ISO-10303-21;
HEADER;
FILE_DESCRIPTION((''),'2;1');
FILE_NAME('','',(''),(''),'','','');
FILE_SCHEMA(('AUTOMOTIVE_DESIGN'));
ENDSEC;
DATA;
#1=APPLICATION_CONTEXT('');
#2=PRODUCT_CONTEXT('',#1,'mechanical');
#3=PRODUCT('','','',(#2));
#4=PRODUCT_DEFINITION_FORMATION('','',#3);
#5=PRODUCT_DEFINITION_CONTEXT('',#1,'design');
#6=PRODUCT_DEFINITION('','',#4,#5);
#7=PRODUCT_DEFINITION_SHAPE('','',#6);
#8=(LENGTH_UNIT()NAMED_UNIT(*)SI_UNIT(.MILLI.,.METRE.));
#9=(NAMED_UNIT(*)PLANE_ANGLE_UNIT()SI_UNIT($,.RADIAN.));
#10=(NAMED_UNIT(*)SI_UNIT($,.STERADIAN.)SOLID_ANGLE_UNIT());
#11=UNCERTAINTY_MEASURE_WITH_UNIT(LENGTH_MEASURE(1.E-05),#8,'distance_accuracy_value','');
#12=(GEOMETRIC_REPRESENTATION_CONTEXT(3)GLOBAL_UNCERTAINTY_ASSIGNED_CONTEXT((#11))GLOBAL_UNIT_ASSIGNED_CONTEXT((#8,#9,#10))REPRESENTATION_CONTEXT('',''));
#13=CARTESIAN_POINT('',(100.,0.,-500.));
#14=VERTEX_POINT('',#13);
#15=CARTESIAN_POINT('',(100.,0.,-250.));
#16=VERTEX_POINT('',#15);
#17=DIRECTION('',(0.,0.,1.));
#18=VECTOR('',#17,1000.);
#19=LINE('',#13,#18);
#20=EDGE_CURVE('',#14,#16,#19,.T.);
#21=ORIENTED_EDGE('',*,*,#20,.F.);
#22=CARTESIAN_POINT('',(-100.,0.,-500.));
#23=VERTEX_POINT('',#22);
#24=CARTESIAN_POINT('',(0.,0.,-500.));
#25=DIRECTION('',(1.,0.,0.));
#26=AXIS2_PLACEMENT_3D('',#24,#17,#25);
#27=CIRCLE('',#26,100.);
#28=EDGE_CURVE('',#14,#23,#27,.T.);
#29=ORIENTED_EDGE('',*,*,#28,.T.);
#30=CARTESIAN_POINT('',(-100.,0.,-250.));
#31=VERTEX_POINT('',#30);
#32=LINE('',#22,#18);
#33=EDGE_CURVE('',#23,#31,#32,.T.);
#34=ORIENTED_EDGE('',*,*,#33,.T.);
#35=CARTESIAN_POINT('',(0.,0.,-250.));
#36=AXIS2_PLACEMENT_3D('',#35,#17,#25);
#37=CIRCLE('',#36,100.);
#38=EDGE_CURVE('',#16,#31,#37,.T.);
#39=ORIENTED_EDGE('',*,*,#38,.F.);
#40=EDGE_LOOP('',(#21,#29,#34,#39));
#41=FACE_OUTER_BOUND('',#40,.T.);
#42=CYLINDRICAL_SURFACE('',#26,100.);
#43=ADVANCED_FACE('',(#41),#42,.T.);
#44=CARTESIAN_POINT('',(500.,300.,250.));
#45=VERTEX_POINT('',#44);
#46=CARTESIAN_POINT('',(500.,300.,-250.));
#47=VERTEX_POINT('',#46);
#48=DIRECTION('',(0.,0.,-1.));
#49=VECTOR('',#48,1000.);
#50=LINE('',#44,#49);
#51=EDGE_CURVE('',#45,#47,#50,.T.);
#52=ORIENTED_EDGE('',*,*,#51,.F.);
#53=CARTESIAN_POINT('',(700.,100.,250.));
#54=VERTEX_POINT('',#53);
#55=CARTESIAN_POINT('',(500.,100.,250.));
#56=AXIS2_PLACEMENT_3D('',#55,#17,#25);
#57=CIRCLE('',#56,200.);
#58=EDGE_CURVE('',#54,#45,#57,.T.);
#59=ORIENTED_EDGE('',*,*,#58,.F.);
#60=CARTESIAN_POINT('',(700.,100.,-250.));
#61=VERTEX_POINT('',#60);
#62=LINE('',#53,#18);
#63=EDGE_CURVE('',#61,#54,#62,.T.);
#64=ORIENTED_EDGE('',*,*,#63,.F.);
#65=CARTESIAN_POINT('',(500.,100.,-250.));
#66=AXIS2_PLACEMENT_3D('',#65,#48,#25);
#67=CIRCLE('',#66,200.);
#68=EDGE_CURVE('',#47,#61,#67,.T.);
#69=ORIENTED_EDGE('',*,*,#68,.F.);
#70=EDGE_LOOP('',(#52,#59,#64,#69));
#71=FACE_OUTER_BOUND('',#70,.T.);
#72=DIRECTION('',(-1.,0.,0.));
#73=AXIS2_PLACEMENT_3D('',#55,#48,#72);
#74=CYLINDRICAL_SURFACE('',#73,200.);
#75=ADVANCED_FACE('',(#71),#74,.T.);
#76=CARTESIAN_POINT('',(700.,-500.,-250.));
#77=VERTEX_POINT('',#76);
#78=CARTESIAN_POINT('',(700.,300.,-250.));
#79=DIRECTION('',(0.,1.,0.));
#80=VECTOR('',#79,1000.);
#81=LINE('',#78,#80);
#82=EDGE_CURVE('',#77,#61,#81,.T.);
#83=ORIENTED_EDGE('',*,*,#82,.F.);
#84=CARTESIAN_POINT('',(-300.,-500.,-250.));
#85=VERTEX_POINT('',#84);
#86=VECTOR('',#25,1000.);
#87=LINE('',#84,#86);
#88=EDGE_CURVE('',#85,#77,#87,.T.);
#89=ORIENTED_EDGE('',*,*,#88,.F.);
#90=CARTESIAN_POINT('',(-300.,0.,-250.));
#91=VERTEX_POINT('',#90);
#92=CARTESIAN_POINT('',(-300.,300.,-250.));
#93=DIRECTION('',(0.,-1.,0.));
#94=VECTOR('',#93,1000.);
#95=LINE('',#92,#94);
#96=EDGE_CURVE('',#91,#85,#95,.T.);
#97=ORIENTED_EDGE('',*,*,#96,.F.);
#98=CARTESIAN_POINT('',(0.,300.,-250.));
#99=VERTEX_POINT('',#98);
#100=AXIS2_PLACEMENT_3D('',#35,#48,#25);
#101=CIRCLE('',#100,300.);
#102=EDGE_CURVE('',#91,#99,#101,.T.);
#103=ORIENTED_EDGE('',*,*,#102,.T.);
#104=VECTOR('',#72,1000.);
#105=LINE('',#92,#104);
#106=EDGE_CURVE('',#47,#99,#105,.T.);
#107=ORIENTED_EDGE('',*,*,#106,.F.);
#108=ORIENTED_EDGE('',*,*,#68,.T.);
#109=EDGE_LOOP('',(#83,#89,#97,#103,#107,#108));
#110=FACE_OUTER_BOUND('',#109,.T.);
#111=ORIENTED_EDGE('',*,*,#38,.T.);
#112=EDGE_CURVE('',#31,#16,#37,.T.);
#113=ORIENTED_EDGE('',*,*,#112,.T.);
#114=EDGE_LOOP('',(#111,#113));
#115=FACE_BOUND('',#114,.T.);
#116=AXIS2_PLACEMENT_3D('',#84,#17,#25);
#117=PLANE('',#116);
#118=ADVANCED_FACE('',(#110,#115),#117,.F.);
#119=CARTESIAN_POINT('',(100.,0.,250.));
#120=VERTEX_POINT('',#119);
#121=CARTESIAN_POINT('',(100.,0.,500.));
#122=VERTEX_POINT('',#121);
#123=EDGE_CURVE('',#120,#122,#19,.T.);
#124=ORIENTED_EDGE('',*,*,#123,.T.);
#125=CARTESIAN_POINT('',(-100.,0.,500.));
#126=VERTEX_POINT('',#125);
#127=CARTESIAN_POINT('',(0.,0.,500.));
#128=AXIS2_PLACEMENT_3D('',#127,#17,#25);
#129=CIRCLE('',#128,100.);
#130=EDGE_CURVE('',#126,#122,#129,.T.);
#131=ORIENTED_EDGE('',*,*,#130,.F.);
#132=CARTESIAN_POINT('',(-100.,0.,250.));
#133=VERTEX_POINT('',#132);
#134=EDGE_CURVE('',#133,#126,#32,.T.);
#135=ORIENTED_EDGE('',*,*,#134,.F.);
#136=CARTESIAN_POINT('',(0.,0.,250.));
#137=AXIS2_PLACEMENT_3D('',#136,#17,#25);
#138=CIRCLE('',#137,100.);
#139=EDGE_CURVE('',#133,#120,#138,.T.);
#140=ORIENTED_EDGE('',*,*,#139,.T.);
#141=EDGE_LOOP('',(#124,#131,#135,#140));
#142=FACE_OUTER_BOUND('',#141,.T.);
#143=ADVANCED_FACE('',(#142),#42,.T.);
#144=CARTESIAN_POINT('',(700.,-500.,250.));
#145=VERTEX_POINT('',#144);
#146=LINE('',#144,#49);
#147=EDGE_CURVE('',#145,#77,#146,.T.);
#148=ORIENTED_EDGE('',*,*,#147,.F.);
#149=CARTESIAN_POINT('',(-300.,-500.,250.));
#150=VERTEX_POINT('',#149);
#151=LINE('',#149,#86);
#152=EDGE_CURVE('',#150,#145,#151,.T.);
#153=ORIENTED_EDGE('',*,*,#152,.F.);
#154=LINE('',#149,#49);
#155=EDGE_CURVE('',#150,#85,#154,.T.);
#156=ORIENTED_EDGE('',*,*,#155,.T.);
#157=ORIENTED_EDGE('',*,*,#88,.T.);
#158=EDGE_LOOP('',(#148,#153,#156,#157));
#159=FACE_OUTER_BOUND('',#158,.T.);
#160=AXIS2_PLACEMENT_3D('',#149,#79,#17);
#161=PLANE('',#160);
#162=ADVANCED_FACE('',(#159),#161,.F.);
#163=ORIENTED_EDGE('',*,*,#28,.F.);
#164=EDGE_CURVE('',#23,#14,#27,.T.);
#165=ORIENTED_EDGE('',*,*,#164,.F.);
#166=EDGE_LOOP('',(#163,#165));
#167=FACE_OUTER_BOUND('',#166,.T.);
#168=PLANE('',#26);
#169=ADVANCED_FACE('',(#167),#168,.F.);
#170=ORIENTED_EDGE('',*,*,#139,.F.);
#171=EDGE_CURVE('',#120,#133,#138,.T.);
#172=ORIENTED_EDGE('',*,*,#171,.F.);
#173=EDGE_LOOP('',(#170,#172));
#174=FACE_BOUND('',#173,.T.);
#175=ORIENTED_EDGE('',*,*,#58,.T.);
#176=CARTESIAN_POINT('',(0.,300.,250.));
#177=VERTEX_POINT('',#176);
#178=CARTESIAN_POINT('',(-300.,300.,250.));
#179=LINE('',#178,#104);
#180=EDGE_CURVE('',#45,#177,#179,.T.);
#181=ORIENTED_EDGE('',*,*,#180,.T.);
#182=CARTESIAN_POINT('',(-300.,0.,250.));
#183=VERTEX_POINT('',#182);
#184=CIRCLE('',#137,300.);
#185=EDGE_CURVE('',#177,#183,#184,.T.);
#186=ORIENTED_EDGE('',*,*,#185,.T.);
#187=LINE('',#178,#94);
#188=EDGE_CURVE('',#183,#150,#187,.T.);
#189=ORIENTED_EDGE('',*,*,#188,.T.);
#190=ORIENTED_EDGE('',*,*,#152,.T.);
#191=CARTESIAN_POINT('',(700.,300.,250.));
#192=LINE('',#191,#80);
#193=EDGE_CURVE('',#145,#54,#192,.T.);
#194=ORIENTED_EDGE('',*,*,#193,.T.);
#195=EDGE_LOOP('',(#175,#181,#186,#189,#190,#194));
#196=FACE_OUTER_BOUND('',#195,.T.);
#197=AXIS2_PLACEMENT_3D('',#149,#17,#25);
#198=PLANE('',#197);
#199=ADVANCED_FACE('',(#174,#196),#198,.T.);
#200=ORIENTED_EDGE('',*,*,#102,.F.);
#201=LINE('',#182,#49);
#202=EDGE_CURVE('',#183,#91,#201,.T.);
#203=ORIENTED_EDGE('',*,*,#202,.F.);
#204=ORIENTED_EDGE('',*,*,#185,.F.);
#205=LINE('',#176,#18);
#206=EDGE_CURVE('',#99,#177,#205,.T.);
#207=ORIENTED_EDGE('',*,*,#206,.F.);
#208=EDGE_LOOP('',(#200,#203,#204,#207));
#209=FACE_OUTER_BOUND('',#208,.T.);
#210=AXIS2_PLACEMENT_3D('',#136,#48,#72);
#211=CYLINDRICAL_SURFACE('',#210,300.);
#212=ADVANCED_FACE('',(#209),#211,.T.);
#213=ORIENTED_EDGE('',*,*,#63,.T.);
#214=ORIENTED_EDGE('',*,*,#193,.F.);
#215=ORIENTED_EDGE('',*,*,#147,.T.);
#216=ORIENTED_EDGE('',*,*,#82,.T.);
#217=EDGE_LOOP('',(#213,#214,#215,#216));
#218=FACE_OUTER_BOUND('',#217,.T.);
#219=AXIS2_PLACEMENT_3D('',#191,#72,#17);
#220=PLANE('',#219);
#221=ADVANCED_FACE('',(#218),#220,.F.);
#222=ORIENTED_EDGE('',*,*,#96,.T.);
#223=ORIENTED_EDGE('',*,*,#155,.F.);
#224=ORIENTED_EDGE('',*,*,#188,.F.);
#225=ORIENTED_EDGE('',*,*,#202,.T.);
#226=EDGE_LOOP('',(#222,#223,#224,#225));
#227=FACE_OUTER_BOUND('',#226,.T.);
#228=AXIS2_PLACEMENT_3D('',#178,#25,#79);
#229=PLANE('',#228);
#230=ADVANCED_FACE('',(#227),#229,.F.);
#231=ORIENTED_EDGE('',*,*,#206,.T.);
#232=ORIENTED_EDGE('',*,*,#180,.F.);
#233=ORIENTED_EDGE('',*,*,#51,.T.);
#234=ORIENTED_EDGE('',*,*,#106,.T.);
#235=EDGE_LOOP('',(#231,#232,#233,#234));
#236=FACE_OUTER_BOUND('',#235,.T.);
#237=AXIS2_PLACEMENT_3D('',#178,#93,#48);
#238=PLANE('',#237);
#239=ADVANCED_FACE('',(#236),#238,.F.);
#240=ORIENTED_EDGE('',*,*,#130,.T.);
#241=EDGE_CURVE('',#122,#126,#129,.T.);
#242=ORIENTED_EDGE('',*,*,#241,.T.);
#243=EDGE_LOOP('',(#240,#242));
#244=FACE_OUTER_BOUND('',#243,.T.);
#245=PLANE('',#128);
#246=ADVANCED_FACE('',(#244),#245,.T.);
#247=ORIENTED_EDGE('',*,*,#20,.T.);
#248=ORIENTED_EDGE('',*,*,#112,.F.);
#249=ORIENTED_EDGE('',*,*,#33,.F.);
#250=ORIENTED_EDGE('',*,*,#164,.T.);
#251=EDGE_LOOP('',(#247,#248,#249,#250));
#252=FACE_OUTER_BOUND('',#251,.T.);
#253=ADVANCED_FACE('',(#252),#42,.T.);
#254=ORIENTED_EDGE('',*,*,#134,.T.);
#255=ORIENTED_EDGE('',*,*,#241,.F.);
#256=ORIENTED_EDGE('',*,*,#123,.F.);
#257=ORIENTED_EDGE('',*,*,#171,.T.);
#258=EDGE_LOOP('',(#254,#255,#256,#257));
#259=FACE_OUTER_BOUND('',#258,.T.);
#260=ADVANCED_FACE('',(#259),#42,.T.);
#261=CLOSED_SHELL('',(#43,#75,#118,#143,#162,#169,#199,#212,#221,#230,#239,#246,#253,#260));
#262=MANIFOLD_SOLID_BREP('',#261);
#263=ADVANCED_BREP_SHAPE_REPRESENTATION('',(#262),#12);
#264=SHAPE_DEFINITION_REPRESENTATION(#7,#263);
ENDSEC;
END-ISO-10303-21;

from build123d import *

# Parameters (mm, degrees)
BOSS_EXTRUDE1_DEPTH      = 250
BOSS_EXTRUDE1_DEPTH_BACK = 250
SKETCH1_W                = 1000
SKETCH1_H                = 800
BOSS_EXTRUDE2_DEPTH      = 500
BOSS_EXTRUDE2_DEPTH_BACK = 500
SKETCH2_R                = 100
FILLET1_R                = 300
FILLET2_R                = 200


with BuildPart() as part:
    # Sketch1 → Boss-Extrude1 (new, two sides: drawn at the far end of the back side and taken through both)
    with BuildSketch(Plane.XY.offset(-BOSS_EXTRUDE1_DEPTH_BACK)):
        with Locations((200, -100)):
            Rectangle(SKETCH1_W, SKETCH1_H)
    extrude(amount=BOSS_EXTRUDE1_DEPTH + BOSS_EXTRUDE1_DEPTH_BACK)

    # Sketch2 → Boss-Extrude2 (add, two sides: drawn at the far end of the back side and taken through both)
    with BuildSketch(Plane.XY.offset(-BOSS_EXTRUDE2_DEPTH_BACK)):
        Circle(SKETCH2_R)
    extrude(amount=BOSS_EXTRUDE2_DEPTH + BOSS_EXTRUDE2_DEPTH_BACK)

    # Fillet1
    fillet1_edges = [part.edges().sort_by_distance(p)[0] for p in [
        (-300, 300, 0),
    ]]
    fillet(fillet1_edges, radius=FILLET1_R)

    # Fillet2
    fillet2_edges = [part.edges().sort_by_distance(p)[0] for p in [
        (700, 300, 0),
    ]]
    fillet(fillet2_edges, radius=FILLET2_R)


solid = part.part
